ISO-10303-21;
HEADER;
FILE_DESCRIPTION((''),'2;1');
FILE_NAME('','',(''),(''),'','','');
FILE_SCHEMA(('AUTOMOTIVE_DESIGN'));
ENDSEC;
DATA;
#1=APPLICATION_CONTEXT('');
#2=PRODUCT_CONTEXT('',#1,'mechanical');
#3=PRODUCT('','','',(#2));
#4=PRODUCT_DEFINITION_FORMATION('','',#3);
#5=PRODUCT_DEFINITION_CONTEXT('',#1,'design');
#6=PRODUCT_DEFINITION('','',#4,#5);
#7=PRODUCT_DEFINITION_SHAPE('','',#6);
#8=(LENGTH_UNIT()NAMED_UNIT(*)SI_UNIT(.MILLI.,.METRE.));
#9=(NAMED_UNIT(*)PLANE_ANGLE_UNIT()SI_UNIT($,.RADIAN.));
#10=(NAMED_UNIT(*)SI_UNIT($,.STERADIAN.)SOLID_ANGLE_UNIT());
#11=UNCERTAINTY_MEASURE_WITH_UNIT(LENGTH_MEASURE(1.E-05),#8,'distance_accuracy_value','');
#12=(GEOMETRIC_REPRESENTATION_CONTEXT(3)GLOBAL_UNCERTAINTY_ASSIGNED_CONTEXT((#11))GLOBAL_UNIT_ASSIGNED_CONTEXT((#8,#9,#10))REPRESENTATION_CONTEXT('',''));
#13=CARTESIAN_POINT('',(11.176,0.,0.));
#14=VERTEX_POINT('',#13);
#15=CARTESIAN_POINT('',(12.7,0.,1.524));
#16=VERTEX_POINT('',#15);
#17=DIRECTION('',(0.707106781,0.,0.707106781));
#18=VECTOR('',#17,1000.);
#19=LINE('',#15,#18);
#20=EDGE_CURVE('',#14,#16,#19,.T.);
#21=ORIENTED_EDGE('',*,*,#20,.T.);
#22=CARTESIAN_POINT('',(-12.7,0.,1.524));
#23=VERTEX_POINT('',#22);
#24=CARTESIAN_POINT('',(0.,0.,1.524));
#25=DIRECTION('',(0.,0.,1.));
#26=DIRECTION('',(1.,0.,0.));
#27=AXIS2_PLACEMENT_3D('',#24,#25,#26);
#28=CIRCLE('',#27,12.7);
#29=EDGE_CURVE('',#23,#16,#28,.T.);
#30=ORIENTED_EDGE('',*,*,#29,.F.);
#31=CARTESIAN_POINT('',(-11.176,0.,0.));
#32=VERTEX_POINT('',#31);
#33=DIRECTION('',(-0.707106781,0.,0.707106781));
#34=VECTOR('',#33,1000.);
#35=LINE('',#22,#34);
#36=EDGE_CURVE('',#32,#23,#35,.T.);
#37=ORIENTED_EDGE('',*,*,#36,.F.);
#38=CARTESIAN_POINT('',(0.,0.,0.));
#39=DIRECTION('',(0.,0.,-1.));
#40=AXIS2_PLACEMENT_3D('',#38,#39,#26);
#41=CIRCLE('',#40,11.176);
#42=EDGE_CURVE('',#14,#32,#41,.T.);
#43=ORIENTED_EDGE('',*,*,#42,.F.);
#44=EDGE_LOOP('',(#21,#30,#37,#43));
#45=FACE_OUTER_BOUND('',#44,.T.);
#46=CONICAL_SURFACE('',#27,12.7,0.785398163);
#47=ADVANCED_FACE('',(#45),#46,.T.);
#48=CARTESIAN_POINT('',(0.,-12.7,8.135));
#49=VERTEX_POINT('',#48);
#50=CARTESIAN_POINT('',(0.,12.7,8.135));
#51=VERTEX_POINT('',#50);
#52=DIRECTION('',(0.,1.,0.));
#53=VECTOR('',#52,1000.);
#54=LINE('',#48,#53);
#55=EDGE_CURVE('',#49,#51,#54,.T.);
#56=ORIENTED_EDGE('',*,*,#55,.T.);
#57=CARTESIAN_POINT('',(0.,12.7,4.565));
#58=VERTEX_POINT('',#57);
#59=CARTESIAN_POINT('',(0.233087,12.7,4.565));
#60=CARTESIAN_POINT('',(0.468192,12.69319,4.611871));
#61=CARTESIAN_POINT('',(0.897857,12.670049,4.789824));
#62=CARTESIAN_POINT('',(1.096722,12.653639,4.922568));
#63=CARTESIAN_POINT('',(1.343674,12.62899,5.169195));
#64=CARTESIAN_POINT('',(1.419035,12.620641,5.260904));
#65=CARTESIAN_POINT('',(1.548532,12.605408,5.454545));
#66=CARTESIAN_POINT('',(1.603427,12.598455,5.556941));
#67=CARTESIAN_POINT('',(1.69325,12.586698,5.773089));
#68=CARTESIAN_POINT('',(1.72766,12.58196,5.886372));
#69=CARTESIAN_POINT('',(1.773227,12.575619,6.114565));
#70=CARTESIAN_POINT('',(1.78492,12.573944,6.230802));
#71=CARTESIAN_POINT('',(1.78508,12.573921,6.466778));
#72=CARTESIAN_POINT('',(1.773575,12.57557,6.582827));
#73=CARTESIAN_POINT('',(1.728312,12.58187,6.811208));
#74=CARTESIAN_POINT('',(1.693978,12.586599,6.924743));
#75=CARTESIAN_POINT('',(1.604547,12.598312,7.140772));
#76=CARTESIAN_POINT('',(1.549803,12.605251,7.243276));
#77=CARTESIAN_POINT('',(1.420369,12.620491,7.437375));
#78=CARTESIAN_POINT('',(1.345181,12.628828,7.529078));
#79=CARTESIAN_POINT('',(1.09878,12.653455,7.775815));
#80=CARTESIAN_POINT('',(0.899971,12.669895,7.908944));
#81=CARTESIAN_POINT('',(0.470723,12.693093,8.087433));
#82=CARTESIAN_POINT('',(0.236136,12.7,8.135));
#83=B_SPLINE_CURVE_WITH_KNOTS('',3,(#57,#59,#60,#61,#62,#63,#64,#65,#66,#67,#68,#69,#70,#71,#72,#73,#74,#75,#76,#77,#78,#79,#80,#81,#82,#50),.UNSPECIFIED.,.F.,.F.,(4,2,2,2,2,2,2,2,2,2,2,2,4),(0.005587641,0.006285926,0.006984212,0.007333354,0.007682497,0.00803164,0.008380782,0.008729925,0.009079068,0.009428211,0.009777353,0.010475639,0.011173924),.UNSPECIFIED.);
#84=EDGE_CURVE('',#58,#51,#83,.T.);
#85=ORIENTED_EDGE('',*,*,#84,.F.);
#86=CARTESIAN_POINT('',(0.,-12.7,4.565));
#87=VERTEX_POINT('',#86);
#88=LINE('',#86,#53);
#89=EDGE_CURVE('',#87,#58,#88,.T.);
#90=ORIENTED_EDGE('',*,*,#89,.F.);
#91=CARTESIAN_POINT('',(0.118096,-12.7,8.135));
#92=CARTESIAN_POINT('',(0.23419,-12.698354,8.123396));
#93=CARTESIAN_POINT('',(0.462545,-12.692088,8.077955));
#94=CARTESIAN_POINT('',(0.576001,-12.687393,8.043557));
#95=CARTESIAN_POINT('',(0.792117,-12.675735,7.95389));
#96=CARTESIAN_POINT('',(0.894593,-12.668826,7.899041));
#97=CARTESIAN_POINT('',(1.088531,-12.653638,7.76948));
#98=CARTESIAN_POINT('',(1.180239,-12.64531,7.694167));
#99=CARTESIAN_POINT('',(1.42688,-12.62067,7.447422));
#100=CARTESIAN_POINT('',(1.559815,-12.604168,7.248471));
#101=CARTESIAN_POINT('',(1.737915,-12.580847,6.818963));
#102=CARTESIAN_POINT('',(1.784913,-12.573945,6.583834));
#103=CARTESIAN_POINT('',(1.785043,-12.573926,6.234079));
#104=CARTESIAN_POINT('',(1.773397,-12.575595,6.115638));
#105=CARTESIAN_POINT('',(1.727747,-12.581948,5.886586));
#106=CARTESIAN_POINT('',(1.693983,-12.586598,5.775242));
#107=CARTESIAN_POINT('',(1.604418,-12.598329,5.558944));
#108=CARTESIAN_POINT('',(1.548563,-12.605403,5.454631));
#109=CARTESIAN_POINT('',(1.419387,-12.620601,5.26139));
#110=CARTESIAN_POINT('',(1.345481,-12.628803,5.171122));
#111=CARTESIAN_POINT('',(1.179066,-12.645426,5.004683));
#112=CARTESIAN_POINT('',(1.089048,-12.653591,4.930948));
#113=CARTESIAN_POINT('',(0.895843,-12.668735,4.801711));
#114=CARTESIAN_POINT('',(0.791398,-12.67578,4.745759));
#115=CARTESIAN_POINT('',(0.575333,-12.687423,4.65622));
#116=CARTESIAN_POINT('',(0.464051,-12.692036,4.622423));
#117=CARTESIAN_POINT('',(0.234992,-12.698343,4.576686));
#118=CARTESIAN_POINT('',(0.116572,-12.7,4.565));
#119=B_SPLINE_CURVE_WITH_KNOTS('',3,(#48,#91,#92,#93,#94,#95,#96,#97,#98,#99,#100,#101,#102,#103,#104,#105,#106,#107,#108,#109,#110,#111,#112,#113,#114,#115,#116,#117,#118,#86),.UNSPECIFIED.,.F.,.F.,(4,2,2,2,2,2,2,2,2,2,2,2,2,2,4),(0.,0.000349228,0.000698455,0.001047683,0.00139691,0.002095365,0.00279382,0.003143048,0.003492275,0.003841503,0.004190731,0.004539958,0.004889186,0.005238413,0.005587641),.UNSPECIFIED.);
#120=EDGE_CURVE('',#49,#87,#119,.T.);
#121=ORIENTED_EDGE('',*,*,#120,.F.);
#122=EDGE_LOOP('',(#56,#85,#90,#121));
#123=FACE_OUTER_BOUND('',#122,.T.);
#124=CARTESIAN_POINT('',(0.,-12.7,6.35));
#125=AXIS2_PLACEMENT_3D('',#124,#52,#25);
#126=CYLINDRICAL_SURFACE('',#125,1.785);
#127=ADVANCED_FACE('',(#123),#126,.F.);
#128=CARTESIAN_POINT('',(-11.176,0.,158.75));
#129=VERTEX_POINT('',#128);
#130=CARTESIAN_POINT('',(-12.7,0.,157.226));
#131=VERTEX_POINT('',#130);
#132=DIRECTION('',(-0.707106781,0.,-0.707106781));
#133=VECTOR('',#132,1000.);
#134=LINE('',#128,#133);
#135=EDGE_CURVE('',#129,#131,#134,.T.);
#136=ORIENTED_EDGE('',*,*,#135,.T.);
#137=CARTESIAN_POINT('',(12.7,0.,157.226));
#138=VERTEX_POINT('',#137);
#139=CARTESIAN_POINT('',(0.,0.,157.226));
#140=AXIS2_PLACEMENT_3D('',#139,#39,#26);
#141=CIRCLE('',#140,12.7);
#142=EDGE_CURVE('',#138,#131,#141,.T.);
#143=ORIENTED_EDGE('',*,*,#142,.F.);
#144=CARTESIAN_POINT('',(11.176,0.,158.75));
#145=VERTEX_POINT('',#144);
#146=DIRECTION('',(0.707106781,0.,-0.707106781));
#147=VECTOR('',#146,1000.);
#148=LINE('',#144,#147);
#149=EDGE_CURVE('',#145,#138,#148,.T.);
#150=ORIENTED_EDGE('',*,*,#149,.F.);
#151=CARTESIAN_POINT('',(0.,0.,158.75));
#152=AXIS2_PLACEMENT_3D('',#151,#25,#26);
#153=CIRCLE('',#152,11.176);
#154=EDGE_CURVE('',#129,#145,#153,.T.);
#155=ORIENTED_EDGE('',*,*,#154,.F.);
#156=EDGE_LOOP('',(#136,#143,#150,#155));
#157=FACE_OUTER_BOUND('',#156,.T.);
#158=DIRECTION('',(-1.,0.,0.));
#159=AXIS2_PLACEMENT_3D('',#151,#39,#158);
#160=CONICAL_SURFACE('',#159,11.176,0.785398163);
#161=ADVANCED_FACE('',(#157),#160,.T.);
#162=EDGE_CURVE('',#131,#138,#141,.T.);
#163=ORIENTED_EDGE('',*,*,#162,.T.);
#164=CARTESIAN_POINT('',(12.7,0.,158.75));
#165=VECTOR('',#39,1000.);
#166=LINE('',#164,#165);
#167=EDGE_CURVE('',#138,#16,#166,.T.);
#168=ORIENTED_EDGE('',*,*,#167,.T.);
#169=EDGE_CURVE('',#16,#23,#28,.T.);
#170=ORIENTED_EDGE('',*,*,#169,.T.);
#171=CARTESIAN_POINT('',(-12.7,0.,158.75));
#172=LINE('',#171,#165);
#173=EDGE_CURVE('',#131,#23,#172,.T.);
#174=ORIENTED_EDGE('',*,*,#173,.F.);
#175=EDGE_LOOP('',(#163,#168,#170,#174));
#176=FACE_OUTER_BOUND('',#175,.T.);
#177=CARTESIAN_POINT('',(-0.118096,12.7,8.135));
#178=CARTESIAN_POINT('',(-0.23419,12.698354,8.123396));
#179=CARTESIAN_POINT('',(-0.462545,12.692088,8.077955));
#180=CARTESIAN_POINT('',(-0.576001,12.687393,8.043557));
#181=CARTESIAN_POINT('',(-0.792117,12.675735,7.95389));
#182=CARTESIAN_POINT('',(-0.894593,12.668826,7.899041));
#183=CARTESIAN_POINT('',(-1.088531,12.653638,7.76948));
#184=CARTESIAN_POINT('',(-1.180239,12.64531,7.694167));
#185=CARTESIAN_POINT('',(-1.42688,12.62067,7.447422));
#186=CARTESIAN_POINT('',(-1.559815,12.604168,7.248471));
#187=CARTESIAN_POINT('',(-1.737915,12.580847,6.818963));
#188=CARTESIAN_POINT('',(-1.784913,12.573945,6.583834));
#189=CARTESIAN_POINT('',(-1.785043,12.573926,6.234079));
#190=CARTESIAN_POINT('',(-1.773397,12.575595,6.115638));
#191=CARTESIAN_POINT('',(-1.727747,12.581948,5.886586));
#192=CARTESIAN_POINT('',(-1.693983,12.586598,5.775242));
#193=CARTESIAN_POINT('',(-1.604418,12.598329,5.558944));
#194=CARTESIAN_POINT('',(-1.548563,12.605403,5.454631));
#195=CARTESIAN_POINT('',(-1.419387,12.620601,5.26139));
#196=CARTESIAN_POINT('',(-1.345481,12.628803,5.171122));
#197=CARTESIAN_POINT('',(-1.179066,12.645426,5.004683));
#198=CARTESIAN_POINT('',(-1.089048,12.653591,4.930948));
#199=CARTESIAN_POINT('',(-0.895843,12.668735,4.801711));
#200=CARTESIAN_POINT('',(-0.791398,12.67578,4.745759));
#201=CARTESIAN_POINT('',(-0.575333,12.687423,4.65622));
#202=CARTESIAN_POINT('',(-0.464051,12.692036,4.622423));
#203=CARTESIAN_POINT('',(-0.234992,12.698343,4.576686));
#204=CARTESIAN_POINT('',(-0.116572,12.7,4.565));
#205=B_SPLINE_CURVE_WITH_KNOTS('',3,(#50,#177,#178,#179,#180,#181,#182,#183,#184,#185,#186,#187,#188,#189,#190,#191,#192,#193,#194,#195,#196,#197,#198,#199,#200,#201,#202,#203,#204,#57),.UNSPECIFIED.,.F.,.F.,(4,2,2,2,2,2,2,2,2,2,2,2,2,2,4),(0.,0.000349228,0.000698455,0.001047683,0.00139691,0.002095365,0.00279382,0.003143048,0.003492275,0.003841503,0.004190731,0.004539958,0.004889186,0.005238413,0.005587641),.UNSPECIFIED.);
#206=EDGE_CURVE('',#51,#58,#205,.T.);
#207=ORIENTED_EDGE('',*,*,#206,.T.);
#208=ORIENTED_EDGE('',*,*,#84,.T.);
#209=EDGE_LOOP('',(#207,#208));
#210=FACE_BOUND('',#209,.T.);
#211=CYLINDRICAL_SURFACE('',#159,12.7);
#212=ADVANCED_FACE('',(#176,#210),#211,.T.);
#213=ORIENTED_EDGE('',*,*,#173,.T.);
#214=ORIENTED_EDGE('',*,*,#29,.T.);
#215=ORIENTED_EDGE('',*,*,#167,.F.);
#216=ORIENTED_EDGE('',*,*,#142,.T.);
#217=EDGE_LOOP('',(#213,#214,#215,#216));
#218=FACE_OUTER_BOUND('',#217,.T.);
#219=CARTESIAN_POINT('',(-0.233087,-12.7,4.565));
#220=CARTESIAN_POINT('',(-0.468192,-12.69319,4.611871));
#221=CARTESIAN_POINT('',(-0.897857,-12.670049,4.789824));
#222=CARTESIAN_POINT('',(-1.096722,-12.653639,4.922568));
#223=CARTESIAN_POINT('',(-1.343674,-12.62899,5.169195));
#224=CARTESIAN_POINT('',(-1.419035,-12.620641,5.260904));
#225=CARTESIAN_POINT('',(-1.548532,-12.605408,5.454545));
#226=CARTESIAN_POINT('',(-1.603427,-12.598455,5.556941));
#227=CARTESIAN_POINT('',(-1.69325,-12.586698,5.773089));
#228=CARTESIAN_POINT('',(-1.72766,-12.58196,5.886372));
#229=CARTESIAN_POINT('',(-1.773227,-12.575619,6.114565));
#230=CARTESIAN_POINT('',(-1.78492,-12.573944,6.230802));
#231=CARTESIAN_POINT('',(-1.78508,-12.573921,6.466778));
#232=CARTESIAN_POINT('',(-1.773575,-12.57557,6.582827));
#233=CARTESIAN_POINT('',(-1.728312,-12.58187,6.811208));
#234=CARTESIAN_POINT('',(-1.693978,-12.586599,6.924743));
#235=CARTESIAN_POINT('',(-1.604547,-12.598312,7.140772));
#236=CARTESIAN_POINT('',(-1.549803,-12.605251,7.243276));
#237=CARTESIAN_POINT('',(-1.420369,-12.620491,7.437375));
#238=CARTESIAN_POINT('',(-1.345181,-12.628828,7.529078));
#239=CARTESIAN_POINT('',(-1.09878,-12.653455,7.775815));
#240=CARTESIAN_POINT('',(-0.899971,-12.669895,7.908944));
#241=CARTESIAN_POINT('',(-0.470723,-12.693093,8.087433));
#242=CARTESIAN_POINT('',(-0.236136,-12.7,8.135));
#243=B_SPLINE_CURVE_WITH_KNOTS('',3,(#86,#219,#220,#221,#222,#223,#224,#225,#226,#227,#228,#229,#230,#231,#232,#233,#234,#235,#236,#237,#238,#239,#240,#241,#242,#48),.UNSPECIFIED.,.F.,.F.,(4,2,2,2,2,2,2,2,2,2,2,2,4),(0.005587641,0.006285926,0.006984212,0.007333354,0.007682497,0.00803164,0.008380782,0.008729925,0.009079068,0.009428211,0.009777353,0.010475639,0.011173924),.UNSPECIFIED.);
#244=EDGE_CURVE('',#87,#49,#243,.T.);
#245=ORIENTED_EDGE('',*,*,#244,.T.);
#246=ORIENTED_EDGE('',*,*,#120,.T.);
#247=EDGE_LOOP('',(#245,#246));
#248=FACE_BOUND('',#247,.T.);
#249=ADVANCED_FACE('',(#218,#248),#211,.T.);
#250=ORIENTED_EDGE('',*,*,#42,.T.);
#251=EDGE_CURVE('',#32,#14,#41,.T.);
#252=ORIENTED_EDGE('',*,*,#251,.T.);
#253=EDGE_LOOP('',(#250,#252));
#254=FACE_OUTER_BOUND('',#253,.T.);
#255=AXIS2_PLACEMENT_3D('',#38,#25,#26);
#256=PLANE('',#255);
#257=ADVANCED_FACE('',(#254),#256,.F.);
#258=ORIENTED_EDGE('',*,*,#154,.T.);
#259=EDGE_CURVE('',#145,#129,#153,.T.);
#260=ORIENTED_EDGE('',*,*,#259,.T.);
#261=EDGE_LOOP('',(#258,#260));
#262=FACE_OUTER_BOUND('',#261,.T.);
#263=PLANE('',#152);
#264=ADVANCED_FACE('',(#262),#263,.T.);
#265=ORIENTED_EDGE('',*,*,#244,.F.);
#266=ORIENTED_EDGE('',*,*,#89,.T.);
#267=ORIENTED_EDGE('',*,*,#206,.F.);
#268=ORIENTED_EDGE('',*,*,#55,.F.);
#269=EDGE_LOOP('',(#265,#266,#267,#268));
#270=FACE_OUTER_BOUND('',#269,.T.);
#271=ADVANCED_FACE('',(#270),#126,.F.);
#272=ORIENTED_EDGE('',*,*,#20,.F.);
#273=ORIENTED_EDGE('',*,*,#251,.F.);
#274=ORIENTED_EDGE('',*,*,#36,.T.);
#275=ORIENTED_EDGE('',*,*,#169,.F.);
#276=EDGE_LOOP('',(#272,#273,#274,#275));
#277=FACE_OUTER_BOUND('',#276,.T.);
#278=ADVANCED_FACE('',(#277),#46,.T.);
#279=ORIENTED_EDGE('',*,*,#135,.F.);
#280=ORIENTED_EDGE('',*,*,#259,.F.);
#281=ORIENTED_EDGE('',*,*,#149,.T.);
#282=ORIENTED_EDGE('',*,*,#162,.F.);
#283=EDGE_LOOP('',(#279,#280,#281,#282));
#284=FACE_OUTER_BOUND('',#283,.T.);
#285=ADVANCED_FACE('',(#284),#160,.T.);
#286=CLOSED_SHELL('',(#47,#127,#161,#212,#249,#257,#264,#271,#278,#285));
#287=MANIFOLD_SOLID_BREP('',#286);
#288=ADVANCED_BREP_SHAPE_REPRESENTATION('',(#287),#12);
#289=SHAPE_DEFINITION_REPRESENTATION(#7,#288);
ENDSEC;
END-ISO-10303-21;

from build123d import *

# Parameters (mm, degrees)
SKETCH1_R               = 12.7
BOSS_EXTRUDE1_DEPTH     = 158.75
CHAMFER1_SIZE           = 1.524
CUT_EXTRUDE1_DEPTH      = 160.762769443
CUT_EXTRUDE1_DEPTH_BACK = 160.762769443
SKETCH2_R               = 1.785


with BuildPart() as part:
    # Sketch1 → Boss-Extrude1 (new body)
    with BuildSketch(Plane.XY):
        with Locations(Location((0, 0, 0), (0, 0, 180))):
            Circle(SKETCH1_R)
    extrude(amount=BOSS_EXTRUDE1_DEPTH)

    # Chamfer1
    chamfer1_edges = [part.edges().sort_by_distance(p)[0] for p in [
        (12.7, 0, 0),
        (12.7, 0, 158.75),
    ]]
    chamfer(chamfer1_edges, length=CHAMFER1_SIZE)

    # Sketch2 → Cut-Extrude1 (cut, two sides: drawn at the far end of the back side and taken through both)
    with BuildSketch(Plane(origin=(0, 0, 0), x_dir=(1, 0, 0), z_dir=(0, 1, 0)).offset(-CUT_EXTRUDE1_DEPTH_BACK)):
        with Locations(Location((0, -6.35, 0), (0, 0, 270))):
            Circle(SKETCH2_R)
    extrude(amount=CUT_EXTRUDE1_DEPTH + CUT_EXTRUDE1_DEPTH_BACK, mode=Mode.SUBTRACT)


solid = part.part
